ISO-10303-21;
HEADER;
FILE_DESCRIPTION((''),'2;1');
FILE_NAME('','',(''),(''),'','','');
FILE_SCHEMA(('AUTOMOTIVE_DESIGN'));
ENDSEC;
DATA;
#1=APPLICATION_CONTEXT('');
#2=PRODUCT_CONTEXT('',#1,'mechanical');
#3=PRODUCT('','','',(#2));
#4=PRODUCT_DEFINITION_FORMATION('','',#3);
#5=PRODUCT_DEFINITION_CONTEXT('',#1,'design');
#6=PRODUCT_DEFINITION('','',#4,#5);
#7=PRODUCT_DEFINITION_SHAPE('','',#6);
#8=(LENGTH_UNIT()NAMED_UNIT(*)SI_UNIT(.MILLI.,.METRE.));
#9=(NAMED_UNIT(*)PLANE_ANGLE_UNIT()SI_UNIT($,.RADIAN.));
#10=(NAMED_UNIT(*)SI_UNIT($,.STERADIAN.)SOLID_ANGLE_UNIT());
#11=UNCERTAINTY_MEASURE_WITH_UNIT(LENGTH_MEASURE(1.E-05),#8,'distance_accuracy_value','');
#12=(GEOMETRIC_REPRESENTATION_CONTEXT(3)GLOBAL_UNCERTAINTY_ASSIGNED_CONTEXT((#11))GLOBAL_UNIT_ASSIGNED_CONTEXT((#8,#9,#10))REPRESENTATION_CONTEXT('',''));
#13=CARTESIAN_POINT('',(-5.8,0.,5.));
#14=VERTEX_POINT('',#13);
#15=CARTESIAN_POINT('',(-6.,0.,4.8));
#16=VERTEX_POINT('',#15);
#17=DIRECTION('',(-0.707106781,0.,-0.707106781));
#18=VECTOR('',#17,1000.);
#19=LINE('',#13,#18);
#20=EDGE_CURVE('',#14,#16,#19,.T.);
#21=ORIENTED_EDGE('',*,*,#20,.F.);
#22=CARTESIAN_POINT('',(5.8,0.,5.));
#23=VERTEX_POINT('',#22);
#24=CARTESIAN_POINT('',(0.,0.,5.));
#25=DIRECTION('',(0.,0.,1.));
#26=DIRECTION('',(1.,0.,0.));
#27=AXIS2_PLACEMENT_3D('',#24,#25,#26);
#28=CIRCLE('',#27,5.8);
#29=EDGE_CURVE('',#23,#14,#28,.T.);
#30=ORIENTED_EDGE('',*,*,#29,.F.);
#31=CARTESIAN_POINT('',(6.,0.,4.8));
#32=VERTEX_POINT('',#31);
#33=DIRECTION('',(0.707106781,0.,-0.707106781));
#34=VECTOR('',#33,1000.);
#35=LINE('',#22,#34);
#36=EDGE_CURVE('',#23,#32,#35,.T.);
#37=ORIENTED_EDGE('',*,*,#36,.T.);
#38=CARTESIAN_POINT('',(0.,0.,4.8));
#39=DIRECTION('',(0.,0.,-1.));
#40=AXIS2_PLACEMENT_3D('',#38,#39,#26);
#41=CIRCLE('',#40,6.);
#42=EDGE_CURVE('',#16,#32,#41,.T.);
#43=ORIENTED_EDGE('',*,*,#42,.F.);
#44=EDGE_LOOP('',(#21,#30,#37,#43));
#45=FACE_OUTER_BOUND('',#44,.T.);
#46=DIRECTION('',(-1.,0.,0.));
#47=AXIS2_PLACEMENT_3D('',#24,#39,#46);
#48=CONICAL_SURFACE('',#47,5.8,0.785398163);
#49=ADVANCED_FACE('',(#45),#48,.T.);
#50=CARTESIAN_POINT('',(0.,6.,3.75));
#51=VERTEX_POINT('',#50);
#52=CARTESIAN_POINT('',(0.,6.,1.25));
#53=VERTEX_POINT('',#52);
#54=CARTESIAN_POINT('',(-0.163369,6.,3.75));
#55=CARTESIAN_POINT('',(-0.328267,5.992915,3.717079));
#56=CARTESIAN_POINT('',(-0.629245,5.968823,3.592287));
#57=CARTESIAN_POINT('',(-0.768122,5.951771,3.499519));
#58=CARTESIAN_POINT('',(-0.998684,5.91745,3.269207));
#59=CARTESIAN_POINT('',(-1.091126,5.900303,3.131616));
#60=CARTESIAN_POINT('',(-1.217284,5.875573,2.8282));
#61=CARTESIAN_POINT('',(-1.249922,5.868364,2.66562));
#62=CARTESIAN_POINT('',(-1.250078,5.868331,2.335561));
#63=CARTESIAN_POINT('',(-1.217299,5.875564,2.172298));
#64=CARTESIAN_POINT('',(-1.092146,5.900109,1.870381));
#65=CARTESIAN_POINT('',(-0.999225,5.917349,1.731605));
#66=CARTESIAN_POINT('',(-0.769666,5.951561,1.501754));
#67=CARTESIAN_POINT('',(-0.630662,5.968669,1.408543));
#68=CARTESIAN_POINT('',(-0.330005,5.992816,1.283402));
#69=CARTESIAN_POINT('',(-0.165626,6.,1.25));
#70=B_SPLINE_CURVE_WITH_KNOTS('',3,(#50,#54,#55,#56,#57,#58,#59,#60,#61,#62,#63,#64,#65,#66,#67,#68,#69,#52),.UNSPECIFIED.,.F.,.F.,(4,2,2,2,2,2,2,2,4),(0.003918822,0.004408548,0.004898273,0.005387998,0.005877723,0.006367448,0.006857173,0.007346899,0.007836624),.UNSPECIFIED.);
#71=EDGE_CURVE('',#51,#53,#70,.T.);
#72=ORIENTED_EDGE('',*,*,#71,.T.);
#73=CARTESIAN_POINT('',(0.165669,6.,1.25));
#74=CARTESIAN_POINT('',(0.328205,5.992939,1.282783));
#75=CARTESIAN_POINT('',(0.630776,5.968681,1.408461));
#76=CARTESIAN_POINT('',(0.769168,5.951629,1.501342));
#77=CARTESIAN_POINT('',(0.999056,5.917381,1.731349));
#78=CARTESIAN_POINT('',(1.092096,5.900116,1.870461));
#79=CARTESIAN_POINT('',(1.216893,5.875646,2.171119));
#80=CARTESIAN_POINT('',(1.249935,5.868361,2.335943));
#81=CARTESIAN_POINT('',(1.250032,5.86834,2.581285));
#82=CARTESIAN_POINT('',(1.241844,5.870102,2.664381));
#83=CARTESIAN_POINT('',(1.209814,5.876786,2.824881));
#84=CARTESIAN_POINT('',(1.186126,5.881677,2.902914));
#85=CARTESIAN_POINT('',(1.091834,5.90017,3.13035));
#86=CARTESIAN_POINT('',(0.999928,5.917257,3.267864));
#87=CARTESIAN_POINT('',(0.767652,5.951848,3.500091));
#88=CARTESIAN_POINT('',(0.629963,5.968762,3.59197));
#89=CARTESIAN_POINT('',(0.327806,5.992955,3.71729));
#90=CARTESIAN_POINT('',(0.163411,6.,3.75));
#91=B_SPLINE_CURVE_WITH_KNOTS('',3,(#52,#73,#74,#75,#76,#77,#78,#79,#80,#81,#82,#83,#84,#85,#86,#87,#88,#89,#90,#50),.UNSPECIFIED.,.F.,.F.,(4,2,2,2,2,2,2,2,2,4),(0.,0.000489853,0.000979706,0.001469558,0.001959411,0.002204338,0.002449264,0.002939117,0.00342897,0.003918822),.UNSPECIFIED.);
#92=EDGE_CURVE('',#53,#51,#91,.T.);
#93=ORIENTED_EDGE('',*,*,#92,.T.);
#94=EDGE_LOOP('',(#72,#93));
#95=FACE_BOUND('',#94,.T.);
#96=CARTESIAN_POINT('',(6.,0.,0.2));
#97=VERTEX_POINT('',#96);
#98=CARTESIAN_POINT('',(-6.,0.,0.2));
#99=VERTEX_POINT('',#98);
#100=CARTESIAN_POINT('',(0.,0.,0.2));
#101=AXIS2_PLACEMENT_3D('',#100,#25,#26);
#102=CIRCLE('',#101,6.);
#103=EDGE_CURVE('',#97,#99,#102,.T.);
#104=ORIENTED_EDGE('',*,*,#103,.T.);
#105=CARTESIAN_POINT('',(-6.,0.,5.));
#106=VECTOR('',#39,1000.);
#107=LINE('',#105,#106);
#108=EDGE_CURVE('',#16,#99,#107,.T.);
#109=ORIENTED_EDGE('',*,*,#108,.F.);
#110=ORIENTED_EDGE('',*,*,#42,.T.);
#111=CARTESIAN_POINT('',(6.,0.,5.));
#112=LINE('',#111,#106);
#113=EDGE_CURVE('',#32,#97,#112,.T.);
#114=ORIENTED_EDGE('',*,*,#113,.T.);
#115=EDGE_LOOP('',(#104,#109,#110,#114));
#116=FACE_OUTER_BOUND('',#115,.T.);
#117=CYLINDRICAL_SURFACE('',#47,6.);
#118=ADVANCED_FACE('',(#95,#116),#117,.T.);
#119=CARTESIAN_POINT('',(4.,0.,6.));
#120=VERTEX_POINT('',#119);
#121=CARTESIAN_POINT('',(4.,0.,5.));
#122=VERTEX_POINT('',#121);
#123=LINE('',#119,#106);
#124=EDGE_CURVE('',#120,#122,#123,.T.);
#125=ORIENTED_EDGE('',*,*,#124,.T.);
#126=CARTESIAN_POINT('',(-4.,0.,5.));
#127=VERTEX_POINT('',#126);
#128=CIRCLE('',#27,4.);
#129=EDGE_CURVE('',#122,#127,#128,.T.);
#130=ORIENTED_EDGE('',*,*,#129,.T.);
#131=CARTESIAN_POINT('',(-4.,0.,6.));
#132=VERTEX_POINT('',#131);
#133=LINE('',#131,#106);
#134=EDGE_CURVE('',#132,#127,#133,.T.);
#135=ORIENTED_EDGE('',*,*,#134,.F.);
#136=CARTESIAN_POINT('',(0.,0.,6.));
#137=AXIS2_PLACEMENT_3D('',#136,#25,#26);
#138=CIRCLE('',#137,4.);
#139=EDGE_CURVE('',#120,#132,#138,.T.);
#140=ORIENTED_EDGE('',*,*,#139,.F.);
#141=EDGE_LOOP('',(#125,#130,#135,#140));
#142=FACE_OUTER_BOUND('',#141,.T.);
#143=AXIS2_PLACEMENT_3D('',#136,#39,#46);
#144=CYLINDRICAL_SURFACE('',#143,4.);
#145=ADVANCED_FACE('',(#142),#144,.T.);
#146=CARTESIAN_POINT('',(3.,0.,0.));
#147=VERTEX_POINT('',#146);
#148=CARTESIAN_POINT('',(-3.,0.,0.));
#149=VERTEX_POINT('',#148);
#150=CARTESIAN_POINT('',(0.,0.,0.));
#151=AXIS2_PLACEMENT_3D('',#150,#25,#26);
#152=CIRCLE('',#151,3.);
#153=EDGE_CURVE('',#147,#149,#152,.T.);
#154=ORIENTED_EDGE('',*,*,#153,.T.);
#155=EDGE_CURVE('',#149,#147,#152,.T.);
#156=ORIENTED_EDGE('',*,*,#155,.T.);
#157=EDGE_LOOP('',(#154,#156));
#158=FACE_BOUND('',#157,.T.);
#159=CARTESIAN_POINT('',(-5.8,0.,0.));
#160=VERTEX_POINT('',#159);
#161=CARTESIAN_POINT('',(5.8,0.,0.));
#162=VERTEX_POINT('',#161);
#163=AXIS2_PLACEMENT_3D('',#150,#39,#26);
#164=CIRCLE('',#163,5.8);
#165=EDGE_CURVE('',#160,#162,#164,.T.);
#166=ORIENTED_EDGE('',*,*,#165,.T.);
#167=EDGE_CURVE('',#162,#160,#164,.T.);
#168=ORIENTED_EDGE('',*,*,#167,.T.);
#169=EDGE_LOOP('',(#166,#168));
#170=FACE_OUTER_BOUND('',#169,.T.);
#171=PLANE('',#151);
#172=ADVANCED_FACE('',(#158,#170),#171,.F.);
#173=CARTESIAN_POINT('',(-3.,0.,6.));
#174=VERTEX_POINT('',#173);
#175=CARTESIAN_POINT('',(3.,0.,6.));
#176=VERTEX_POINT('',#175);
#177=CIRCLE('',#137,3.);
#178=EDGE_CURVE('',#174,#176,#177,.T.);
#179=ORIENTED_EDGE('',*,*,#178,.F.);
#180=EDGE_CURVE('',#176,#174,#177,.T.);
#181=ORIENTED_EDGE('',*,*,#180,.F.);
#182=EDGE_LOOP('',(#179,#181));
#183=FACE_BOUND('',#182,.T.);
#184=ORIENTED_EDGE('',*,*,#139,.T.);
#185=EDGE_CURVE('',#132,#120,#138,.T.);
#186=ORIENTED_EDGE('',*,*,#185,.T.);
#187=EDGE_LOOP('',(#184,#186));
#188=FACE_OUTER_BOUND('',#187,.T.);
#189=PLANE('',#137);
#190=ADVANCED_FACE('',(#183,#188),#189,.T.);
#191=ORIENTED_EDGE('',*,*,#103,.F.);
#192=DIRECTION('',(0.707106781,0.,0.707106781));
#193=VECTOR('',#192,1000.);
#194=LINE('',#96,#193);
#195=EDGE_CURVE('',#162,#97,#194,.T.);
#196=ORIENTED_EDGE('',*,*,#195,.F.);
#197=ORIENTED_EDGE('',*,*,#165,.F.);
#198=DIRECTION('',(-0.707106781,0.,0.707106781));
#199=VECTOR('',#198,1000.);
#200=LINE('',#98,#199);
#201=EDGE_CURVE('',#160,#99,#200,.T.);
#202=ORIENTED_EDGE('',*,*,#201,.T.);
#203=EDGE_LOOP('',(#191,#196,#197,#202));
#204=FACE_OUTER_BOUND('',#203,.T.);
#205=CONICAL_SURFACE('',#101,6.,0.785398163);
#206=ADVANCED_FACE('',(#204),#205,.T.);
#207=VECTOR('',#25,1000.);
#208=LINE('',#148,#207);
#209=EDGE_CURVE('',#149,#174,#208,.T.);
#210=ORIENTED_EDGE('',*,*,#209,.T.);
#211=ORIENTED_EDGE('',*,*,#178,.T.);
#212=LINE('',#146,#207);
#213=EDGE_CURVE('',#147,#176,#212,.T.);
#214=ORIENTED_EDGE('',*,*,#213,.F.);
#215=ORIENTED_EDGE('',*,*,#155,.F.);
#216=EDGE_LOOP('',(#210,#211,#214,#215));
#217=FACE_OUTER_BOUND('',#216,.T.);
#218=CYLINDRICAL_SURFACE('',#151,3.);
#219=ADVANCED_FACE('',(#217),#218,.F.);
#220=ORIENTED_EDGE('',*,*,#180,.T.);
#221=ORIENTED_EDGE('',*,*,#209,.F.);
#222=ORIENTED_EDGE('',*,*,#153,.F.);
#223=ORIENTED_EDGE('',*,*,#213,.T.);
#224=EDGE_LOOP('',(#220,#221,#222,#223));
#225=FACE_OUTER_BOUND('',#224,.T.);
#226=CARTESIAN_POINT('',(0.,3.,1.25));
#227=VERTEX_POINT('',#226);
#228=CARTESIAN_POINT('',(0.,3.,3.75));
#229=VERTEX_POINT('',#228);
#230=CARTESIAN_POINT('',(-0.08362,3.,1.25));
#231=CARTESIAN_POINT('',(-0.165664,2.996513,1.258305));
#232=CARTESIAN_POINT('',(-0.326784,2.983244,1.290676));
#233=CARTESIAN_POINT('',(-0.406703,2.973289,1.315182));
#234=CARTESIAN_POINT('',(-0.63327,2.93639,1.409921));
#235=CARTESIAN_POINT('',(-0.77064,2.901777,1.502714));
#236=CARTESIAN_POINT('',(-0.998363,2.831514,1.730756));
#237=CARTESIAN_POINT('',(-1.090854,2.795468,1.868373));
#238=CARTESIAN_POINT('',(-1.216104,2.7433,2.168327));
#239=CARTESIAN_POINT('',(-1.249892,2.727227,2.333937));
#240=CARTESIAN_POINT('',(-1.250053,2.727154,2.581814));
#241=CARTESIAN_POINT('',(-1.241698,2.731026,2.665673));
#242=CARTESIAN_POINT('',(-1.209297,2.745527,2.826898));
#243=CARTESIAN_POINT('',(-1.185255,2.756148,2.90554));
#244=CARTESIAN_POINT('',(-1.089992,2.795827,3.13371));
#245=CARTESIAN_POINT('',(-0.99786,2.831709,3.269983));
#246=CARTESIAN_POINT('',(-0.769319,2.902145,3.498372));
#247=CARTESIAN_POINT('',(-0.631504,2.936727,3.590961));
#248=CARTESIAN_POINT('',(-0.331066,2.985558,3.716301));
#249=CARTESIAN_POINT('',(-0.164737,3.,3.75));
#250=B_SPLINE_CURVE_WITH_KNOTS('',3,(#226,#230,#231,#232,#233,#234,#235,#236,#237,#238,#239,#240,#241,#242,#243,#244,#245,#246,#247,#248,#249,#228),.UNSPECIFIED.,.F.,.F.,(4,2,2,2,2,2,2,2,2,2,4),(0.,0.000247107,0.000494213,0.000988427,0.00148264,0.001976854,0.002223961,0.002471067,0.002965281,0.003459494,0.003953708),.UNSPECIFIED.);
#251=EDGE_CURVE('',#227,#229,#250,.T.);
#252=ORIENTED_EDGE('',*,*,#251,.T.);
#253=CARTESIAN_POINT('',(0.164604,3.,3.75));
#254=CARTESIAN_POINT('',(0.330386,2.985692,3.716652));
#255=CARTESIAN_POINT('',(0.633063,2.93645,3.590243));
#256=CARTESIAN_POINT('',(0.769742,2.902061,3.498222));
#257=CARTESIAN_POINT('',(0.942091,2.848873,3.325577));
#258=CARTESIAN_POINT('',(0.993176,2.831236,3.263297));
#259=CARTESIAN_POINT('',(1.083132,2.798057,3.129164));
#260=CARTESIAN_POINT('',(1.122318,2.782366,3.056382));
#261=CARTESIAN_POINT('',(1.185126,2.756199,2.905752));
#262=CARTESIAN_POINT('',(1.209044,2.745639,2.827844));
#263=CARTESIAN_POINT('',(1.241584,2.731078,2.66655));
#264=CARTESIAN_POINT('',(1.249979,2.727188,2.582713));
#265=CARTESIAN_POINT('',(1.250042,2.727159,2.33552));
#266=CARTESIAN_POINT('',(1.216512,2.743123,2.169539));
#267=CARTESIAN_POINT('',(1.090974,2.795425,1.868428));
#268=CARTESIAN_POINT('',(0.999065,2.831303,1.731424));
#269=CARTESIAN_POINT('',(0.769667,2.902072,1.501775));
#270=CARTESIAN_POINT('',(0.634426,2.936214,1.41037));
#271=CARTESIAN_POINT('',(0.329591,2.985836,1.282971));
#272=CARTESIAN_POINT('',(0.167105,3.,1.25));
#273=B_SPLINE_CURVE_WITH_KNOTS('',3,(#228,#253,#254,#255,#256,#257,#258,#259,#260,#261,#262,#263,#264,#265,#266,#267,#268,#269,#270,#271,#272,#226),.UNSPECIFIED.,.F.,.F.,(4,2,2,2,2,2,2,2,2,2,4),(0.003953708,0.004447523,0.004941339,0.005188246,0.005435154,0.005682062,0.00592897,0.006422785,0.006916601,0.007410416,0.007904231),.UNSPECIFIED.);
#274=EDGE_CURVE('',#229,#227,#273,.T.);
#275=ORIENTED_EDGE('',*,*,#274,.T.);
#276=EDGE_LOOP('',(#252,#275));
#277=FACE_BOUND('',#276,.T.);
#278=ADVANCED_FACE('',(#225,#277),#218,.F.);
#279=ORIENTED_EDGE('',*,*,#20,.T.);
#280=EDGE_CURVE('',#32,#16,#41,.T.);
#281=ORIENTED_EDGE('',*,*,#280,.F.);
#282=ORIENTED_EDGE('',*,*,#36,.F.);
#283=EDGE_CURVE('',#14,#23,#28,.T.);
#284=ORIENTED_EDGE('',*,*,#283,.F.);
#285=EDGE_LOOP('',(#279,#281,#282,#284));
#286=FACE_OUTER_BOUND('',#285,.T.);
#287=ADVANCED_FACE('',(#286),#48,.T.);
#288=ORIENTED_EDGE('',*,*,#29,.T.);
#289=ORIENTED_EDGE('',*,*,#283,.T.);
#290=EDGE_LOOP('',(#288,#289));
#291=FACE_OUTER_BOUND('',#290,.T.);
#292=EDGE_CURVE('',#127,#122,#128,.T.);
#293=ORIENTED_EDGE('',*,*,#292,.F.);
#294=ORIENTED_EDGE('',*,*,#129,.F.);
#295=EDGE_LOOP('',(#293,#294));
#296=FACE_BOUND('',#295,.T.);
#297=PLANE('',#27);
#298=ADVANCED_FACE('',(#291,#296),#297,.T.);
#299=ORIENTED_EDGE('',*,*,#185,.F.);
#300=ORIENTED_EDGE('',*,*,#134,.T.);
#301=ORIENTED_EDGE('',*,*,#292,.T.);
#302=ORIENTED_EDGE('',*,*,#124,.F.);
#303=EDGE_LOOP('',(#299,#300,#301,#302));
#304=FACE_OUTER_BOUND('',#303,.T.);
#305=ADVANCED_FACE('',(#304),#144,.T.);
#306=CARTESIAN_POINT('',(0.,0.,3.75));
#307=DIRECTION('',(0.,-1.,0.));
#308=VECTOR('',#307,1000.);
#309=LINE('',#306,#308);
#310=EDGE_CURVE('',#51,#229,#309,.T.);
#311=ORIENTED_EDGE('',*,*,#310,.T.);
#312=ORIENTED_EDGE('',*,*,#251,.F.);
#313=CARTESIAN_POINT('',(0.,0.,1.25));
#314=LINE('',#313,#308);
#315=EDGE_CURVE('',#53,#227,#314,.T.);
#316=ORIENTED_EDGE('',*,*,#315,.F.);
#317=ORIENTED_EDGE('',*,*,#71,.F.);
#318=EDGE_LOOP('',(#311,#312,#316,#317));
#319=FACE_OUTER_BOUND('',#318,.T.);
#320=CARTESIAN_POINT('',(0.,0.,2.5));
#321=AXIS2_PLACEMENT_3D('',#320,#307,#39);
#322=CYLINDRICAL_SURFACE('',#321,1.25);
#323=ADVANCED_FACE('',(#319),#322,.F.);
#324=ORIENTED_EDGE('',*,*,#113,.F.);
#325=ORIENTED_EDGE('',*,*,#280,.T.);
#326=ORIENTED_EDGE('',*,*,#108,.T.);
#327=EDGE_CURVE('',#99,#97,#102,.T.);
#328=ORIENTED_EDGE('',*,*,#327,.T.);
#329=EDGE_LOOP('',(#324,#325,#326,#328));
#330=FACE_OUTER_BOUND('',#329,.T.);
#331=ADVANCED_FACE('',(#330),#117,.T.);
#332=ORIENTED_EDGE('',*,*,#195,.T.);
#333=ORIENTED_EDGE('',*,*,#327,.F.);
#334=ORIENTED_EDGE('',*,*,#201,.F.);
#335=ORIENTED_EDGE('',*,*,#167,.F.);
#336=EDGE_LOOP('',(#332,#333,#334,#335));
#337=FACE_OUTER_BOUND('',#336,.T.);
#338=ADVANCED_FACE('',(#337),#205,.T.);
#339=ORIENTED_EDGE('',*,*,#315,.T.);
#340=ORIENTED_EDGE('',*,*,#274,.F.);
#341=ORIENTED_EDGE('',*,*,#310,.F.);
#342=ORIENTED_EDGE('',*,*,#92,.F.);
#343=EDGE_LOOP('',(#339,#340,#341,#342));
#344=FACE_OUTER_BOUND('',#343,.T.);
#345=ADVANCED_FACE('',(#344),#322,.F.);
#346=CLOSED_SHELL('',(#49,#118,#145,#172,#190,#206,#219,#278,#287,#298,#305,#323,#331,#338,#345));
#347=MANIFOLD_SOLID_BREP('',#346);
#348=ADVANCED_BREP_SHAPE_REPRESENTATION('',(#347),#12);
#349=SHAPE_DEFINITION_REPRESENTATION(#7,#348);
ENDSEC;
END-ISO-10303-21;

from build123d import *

# Parameters (mm, degrees)
SKETCH1_R           = 6
BOSS_EXTRUDE1_DEPTH = 5
SKETCH2_R           = 4
BOSS_EXTRUDE2_DEPTH = 1
SKETCH3_R           = 3
CUT_EXTRUDE1_DEPTH  = 11.392304845
CHAMFER1_SIZE       = 0.2


with BuildPart() as part:
    # Sketch1 → Boss-Extrude1 (new body)
    with BuildSketch(Plane.XY):
        Circle(SKETCH1_R)
    extrude(amount=BOSS_EXTRUDE1_DEPTH)

    # Sketch2 → Boss-Extrude2 (add)
    with BuildSketch(Plane.XY.offset(5)):
        Circle(SKETCH2_R)
    extrude(amount=BOSS_EXTRUDE2_DEPTH)

    # Sketch3 → Cut-Extrude1 (cut, through all)
    with BuildSketch(Plane.XY.offset(6)):
        Circle(SKETCH3_R)
    extrude(amount=-CUT_EXTRUDE1_DEPTH, mode=Mode.SUBTRACT)

    # Chamfer1
    chamfer1_edges = [part.edges().sort_by_distance(p)[0] for p in [
        (-6, 0, 0),
        (-6, 0, 5),
    ]]
    chamfer(chamfer1_edges, length=CHAMFER1_SIZE)

    # Sketch4 → M3 Tapped Hole1 (revolve, cut)
    with BuildSketch(Plane(origin=(0, 0, 2.5), x_dir=(0, 0, -1), z_dir=(1, 0, 0))):
        Polygon((0, 0), (0, 8.251075774), (1.25, 7.5), (1.25, 0), align=None)
    revolve(axis=Axis((0, -6.35, 2.5), (0, 1, 0)), mode=Mode.SUBTRACT)


solid = part.part
